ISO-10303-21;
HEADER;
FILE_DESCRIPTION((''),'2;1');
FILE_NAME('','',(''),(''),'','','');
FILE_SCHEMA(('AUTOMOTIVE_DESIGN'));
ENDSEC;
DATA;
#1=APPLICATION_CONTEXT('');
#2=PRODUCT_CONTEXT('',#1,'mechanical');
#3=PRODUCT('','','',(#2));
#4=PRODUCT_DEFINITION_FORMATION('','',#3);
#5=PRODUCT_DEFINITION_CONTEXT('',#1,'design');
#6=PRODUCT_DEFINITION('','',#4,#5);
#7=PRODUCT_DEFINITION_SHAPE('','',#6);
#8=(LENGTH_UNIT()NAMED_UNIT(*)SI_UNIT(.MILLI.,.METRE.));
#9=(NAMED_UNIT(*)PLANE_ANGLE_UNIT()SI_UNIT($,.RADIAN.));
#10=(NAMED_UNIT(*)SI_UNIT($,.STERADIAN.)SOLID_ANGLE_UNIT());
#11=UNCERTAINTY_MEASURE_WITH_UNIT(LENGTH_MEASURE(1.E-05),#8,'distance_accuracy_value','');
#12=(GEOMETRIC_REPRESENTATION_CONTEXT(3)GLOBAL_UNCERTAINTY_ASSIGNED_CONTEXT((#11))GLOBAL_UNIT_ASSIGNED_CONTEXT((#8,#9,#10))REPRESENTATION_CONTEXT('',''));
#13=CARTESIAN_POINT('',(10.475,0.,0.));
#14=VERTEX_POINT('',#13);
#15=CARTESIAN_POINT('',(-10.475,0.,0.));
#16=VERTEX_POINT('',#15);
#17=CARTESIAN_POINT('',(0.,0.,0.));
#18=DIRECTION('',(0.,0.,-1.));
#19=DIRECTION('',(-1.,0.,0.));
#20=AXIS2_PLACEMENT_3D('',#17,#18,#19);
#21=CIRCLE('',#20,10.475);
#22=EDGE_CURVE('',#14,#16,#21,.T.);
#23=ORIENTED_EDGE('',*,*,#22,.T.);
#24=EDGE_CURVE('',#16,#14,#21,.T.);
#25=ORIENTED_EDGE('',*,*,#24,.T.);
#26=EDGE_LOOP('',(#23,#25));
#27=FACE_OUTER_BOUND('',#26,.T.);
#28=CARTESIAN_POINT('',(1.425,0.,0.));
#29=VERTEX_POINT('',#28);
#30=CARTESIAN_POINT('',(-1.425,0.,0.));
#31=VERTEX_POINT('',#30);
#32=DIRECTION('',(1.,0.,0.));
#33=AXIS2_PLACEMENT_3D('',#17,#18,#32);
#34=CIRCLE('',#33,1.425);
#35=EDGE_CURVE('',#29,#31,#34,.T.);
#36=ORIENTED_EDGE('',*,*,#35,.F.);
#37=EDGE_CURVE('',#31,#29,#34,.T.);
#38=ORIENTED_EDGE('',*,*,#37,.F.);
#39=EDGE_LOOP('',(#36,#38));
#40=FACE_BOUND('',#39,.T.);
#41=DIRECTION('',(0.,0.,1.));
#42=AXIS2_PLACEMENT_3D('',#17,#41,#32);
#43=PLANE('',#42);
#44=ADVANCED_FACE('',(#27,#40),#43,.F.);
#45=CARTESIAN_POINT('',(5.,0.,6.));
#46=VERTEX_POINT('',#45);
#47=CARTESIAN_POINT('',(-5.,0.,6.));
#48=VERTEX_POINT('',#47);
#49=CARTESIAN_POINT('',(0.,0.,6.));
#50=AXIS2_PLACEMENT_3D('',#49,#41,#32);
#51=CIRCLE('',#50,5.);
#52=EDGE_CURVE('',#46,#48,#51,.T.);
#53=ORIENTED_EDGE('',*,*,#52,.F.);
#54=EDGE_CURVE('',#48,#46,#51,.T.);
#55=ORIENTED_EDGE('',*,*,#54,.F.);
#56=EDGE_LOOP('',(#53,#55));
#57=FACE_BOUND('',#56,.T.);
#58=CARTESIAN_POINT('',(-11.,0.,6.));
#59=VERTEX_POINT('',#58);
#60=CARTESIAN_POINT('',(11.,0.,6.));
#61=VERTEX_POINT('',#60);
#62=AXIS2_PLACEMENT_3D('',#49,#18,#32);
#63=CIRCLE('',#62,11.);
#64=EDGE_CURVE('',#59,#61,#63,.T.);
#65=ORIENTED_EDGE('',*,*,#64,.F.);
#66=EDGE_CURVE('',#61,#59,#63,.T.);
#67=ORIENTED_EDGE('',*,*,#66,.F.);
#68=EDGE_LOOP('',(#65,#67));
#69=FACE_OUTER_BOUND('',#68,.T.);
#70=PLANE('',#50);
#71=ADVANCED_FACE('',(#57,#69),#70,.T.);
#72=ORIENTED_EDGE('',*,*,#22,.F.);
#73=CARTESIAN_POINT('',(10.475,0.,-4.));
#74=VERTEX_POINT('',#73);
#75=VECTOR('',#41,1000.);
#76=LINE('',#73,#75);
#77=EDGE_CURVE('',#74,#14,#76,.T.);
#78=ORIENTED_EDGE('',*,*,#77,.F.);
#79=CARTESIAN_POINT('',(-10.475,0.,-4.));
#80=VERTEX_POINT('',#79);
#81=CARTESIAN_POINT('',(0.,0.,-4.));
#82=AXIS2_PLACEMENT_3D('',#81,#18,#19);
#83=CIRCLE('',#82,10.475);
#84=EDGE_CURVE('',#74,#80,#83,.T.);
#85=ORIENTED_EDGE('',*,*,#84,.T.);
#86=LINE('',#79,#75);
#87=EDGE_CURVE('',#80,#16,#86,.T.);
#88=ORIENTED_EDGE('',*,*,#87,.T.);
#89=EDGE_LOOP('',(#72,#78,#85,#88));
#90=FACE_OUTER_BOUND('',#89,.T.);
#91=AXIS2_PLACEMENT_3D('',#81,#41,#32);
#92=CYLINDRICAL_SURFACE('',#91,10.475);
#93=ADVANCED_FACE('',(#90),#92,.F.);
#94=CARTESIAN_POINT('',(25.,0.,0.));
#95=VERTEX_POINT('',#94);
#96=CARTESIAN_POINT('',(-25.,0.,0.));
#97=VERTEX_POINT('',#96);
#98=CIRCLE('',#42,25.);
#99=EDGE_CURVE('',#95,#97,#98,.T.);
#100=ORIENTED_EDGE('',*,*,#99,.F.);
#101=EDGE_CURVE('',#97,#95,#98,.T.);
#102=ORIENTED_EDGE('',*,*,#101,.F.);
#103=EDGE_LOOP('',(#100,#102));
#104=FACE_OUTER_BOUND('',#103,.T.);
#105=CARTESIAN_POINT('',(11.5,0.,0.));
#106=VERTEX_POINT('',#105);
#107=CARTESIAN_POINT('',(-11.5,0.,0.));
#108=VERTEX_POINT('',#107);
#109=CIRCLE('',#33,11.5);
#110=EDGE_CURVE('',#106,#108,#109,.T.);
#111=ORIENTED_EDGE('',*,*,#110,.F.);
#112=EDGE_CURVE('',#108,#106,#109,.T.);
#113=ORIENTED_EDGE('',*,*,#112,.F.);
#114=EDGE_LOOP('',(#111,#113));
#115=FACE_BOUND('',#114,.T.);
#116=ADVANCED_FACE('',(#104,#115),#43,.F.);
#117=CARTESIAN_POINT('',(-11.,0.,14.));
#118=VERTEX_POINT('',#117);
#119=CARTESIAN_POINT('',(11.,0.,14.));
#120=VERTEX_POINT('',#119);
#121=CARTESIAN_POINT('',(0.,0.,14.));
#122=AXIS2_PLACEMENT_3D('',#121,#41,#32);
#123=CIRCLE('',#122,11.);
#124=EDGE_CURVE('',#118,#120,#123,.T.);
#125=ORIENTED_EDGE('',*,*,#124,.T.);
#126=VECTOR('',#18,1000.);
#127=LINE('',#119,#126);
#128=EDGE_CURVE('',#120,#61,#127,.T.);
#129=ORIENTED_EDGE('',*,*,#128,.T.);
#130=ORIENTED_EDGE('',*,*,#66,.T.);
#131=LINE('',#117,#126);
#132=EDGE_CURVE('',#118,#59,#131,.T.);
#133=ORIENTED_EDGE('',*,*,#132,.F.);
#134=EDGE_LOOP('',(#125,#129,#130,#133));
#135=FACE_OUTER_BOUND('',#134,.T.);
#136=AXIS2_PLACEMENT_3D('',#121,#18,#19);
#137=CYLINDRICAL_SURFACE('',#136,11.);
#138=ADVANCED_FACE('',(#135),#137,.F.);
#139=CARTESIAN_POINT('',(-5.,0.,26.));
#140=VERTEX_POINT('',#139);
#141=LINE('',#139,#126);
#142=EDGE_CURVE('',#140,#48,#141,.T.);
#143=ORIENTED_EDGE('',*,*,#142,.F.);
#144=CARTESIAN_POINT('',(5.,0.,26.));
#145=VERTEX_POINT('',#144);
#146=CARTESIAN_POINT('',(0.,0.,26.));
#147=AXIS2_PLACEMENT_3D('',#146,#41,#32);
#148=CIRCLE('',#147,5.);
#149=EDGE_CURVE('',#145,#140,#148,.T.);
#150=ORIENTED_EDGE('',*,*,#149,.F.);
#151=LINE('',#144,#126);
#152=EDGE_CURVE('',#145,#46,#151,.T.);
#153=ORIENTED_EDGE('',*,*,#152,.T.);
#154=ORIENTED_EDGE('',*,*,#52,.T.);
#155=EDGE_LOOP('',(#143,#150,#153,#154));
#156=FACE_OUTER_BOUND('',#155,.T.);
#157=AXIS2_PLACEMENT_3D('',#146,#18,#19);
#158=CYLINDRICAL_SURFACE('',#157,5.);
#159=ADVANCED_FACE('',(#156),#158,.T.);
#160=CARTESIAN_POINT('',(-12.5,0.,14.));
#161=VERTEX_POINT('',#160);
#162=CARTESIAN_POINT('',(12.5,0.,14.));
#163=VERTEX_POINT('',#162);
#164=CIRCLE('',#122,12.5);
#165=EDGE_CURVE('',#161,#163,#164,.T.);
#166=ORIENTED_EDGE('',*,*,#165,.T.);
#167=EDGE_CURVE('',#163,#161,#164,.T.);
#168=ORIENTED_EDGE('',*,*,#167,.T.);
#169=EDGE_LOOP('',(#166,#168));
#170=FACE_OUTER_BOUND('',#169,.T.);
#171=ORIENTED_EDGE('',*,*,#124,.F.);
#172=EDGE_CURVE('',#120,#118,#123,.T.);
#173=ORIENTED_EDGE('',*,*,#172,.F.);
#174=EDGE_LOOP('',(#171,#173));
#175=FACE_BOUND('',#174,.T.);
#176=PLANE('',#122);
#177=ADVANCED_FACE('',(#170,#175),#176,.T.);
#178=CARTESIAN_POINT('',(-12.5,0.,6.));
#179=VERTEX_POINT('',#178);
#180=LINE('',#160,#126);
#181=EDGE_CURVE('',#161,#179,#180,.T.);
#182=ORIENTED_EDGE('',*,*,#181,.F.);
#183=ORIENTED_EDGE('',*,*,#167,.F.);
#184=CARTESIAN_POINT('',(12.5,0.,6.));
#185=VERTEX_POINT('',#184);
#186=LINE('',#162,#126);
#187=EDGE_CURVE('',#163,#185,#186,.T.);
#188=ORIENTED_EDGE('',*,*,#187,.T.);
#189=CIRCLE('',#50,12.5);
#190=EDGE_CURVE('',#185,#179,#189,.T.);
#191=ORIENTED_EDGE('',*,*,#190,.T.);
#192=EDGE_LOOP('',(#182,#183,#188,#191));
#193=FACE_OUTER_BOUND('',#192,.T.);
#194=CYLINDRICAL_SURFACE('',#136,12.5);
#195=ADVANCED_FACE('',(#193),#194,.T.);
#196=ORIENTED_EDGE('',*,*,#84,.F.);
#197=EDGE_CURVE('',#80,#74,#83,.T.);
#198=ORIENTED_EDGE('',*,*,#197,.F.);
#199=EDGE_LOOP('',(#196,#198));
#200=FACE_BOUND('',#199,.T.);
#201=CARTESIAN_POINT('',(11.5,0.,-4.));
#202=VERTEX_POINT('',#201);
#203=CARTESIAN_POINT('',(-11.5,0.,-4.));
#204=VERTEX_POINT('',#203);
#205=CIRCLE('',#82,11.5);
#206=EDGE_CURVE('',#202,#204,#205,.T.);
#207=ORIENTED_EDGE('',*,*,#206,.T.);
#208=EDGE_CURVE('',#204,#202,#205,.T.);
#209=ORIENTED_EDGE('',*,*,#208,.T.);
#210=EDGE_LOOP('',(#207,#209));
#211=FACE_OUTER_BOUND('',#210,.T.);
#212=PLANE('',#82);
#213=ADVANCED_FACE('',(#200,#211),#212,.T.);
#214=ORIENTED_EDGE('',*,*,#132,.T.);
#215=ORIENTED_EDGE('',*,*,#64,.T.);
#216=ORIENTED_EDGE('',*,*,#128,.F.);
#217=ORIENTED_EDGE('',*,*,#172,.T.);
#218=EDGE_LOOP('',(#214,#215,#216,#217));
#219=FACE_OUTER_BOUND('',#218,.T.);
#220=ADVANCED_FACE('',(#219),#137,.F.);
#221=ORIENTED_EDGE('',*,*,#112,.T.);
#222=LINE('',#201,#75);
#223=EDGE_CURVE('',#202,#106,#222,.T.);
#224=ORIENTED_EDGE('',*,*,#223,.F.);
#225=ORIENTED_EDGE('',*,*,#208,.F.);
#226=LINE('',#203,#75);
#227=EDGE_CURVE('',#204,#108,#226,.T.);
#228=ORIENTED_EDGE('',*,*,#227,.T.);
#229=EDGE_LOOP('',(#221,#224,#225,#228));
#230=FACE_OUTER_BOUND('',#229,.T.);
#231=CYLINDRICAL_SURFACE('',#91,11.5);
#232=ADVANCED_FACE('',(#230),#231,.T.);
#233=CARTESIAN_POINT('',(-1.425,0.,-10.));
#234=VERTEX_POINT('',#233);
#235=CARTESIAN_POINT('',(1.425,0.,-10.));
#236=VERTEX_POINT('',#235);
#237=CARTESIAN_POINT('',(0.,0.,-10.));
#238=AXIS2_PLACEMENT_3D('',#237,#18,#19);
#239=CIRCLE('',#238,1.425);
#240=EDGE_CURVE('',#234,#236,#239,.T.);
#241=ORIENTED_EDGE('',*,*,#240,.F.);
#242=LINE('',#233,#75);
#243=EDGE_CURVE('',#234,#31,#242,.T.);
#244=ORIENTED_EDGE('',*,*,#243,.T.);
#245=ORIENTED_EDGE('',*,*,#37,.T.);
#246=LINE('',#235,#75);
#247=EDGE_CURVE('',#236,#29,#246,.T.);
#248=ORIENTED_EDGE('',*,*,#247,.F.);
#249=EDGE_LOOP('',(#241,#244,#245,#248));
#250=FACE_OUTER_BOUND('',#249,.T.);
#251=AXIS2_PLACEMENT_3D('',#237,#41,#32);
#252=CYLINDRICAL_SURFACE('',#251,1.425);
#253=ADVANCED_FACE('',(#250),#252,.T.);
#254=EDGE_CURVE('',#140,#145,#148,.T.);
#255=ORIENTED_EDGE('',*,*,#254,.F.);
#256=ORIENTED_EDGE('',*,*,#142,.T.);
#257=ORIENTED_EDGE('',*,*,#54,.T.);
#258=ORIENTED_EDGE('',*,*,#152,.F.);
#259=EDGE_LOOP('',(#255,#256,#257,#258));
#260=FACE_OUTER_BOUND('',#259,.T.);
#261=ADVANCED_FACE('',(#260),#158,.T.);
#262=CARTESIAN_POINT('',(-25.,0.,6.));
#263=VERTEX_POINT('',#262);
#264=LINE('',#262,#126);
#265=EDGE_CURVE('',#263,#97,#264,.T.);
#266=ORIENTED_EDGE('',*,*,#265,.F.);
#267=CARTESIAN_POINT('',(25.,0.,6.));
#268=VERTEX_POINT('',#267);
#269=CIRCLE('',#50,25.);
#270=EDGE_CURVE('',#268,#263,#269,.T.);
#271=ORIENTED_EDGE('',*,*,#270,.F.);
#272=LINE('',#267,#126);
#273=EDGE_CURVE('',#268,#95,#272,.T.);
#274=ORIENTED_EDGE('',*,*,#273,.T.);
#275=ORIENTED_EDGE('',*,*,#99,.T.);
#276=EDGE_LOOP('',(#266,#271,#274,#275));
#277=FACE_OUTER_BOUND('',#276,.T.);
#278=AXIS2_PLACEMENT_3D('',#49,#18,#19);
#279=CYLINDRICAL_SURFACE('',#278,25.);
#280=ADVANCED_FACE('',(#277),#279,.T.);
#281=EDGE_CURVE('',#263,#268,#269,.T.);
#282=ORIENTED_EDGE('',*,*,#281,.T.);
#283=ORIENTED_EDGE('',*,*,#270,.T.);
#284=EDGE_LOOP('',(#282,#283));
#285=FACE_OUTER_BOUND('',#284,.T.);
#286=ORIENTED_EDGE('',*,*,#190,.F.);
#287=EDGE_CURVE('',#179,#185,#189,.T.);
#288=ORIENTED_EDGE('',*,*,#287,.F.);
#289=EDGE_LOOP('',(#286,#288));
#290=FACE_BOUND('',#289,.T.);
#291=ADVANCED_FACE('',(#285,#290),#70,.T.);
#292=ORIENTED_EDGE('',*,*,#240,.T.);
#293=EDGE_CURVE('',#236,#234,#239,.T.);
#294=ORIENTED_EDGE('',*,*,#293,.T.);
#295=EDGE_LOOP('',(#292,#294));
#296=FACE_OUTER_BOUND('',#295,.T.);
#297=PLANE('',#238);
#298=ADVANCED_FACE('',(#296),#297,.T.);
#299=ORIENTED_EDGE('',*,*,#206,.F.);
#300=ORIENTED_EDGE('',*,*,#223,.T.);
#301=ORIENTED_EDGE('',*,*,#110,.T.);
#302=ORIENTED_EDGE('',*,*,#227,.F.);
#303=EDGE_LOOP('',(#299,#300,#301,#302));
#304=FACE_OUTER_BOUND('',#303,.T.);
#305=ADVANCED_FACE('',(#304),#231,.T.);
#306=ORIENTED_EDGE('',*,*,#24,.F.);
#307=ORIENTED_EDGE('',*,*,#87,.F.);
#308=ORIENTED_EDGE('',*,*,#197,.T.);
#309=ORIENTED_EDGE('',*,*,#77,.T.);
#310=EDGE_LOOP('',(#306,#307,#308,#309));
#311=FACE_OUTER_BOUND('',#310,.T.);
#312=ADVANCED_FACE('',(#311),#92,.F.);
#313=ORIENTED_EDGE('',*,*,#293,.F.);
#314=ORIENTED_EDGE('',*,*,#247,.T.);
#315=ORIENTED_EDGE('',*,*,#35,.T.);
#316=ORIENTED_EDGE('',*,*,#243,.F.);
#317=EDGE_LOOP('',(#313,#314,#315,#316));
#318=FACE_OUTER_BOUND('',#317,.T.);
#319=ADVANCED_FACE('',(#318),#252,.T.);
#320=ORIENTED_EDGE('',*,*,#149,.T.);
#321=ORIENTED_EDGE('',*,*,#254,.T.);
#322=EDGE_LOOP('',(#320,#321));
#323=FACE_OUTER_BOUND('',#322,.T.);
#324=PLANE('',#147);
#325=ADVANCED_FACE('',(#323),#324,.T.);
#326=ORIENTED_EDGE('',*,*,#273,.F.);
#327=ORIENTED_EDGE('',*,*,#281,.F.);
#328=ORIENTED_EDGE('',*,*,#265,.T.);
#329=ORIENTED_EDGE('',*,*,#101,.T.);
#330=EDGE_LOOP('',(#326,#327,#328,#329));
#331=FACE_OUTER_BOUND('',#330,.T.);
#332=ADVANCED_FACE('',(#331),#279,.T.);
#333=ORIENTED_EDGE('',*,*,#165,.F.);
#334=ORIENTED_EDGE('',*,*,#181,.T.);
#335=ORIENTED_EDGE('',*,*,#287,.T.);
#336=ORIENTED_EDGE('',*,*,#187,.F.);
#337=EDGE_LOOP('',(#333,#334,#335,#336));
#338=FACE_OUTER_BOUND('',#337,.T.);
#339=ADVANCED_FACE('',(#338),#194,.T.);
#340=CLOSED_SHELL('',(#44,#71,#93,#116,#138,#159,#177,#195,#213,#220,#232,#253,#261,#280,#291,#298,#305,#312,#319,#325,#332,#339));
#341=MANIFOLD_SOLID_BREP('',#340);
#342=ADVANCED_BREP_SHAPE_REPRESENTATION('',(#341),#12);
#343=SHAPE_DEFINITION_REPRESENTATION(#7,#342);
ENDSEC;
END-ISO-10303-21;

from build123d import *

# Parameters (mm, degrees)
SKETCH_1_R      = 25
EXTRUDE_1_DEPTH = 6
SKETCH_2_R      = 12.5
SKETCH_2_R_2    = 11
EXTRUDE_2_DEPTH = 8
SKETCH_3_R      = 5
EXTRUDE_3_DEPTH = 20
SKETCH_5_R      = 11.5
SKETCH_5_R_2    = 10.475
EXTRUDE_4_DEPTH = 4
SKETCH_6_R      = 1.425
EXTRUDE_5_DEPTH = 10


with BuildPart() as part:
    # 草图1 → 凸台-拉伸1 (new body)
    with BuildSketch(Plane.XY):
        Circle(SKETCH_1_R)
    extrude(amount=EXTRUDE_1_DEPTH)

    # 草图2 → 凸台-拉伸2 (add)
    with BuildSketch(Plane.XY.offset(6)):
        Circle(SKETCH_2_R)
        Circle(SKETCH_2_R_2, mode=Mode.SUBTRACT)
    extrude(amount=EXTRUDE_2_DEPTH)

    # 草图3 → 凸台-拉伸3 (add)
    with BuildSketch(Plane.XY.offset(6)):
        Circle(SKETCH_3_R)
    extrude(amount=EXTRUDE_3_DEPTH)

    # 草图5 → 凸台-拉伸4 (add)
    with BuildSketch(Plane(origin=(0, 0, 0), x_dir=(-1, 0, 0), z_dir=(0, 0, -1))):
        with Locations(Location((0, 0, 0), (0, 0, 180))):
            Circle(SKETCH_5_R)
        Circle(SKETCH_5_R_2, mode=Mode.SUBTRACT)
    extrude(amount=EXTRUDE_4_DEPTH)

    # 草图6 → 凸台-拉伸5 (add)
    with BuildSketch(Plane(origin=(0, 0, 0), x_dir=(-1, 0, 0), z_dir=(0, 0, -1))):
        with Locations(Location((0, 0, 0), (0, 0, 180))):
            Circle(SKETCH_6_R)
    extrude(amount=EXTRUDE_5_DEPTH)


solid = part.part
